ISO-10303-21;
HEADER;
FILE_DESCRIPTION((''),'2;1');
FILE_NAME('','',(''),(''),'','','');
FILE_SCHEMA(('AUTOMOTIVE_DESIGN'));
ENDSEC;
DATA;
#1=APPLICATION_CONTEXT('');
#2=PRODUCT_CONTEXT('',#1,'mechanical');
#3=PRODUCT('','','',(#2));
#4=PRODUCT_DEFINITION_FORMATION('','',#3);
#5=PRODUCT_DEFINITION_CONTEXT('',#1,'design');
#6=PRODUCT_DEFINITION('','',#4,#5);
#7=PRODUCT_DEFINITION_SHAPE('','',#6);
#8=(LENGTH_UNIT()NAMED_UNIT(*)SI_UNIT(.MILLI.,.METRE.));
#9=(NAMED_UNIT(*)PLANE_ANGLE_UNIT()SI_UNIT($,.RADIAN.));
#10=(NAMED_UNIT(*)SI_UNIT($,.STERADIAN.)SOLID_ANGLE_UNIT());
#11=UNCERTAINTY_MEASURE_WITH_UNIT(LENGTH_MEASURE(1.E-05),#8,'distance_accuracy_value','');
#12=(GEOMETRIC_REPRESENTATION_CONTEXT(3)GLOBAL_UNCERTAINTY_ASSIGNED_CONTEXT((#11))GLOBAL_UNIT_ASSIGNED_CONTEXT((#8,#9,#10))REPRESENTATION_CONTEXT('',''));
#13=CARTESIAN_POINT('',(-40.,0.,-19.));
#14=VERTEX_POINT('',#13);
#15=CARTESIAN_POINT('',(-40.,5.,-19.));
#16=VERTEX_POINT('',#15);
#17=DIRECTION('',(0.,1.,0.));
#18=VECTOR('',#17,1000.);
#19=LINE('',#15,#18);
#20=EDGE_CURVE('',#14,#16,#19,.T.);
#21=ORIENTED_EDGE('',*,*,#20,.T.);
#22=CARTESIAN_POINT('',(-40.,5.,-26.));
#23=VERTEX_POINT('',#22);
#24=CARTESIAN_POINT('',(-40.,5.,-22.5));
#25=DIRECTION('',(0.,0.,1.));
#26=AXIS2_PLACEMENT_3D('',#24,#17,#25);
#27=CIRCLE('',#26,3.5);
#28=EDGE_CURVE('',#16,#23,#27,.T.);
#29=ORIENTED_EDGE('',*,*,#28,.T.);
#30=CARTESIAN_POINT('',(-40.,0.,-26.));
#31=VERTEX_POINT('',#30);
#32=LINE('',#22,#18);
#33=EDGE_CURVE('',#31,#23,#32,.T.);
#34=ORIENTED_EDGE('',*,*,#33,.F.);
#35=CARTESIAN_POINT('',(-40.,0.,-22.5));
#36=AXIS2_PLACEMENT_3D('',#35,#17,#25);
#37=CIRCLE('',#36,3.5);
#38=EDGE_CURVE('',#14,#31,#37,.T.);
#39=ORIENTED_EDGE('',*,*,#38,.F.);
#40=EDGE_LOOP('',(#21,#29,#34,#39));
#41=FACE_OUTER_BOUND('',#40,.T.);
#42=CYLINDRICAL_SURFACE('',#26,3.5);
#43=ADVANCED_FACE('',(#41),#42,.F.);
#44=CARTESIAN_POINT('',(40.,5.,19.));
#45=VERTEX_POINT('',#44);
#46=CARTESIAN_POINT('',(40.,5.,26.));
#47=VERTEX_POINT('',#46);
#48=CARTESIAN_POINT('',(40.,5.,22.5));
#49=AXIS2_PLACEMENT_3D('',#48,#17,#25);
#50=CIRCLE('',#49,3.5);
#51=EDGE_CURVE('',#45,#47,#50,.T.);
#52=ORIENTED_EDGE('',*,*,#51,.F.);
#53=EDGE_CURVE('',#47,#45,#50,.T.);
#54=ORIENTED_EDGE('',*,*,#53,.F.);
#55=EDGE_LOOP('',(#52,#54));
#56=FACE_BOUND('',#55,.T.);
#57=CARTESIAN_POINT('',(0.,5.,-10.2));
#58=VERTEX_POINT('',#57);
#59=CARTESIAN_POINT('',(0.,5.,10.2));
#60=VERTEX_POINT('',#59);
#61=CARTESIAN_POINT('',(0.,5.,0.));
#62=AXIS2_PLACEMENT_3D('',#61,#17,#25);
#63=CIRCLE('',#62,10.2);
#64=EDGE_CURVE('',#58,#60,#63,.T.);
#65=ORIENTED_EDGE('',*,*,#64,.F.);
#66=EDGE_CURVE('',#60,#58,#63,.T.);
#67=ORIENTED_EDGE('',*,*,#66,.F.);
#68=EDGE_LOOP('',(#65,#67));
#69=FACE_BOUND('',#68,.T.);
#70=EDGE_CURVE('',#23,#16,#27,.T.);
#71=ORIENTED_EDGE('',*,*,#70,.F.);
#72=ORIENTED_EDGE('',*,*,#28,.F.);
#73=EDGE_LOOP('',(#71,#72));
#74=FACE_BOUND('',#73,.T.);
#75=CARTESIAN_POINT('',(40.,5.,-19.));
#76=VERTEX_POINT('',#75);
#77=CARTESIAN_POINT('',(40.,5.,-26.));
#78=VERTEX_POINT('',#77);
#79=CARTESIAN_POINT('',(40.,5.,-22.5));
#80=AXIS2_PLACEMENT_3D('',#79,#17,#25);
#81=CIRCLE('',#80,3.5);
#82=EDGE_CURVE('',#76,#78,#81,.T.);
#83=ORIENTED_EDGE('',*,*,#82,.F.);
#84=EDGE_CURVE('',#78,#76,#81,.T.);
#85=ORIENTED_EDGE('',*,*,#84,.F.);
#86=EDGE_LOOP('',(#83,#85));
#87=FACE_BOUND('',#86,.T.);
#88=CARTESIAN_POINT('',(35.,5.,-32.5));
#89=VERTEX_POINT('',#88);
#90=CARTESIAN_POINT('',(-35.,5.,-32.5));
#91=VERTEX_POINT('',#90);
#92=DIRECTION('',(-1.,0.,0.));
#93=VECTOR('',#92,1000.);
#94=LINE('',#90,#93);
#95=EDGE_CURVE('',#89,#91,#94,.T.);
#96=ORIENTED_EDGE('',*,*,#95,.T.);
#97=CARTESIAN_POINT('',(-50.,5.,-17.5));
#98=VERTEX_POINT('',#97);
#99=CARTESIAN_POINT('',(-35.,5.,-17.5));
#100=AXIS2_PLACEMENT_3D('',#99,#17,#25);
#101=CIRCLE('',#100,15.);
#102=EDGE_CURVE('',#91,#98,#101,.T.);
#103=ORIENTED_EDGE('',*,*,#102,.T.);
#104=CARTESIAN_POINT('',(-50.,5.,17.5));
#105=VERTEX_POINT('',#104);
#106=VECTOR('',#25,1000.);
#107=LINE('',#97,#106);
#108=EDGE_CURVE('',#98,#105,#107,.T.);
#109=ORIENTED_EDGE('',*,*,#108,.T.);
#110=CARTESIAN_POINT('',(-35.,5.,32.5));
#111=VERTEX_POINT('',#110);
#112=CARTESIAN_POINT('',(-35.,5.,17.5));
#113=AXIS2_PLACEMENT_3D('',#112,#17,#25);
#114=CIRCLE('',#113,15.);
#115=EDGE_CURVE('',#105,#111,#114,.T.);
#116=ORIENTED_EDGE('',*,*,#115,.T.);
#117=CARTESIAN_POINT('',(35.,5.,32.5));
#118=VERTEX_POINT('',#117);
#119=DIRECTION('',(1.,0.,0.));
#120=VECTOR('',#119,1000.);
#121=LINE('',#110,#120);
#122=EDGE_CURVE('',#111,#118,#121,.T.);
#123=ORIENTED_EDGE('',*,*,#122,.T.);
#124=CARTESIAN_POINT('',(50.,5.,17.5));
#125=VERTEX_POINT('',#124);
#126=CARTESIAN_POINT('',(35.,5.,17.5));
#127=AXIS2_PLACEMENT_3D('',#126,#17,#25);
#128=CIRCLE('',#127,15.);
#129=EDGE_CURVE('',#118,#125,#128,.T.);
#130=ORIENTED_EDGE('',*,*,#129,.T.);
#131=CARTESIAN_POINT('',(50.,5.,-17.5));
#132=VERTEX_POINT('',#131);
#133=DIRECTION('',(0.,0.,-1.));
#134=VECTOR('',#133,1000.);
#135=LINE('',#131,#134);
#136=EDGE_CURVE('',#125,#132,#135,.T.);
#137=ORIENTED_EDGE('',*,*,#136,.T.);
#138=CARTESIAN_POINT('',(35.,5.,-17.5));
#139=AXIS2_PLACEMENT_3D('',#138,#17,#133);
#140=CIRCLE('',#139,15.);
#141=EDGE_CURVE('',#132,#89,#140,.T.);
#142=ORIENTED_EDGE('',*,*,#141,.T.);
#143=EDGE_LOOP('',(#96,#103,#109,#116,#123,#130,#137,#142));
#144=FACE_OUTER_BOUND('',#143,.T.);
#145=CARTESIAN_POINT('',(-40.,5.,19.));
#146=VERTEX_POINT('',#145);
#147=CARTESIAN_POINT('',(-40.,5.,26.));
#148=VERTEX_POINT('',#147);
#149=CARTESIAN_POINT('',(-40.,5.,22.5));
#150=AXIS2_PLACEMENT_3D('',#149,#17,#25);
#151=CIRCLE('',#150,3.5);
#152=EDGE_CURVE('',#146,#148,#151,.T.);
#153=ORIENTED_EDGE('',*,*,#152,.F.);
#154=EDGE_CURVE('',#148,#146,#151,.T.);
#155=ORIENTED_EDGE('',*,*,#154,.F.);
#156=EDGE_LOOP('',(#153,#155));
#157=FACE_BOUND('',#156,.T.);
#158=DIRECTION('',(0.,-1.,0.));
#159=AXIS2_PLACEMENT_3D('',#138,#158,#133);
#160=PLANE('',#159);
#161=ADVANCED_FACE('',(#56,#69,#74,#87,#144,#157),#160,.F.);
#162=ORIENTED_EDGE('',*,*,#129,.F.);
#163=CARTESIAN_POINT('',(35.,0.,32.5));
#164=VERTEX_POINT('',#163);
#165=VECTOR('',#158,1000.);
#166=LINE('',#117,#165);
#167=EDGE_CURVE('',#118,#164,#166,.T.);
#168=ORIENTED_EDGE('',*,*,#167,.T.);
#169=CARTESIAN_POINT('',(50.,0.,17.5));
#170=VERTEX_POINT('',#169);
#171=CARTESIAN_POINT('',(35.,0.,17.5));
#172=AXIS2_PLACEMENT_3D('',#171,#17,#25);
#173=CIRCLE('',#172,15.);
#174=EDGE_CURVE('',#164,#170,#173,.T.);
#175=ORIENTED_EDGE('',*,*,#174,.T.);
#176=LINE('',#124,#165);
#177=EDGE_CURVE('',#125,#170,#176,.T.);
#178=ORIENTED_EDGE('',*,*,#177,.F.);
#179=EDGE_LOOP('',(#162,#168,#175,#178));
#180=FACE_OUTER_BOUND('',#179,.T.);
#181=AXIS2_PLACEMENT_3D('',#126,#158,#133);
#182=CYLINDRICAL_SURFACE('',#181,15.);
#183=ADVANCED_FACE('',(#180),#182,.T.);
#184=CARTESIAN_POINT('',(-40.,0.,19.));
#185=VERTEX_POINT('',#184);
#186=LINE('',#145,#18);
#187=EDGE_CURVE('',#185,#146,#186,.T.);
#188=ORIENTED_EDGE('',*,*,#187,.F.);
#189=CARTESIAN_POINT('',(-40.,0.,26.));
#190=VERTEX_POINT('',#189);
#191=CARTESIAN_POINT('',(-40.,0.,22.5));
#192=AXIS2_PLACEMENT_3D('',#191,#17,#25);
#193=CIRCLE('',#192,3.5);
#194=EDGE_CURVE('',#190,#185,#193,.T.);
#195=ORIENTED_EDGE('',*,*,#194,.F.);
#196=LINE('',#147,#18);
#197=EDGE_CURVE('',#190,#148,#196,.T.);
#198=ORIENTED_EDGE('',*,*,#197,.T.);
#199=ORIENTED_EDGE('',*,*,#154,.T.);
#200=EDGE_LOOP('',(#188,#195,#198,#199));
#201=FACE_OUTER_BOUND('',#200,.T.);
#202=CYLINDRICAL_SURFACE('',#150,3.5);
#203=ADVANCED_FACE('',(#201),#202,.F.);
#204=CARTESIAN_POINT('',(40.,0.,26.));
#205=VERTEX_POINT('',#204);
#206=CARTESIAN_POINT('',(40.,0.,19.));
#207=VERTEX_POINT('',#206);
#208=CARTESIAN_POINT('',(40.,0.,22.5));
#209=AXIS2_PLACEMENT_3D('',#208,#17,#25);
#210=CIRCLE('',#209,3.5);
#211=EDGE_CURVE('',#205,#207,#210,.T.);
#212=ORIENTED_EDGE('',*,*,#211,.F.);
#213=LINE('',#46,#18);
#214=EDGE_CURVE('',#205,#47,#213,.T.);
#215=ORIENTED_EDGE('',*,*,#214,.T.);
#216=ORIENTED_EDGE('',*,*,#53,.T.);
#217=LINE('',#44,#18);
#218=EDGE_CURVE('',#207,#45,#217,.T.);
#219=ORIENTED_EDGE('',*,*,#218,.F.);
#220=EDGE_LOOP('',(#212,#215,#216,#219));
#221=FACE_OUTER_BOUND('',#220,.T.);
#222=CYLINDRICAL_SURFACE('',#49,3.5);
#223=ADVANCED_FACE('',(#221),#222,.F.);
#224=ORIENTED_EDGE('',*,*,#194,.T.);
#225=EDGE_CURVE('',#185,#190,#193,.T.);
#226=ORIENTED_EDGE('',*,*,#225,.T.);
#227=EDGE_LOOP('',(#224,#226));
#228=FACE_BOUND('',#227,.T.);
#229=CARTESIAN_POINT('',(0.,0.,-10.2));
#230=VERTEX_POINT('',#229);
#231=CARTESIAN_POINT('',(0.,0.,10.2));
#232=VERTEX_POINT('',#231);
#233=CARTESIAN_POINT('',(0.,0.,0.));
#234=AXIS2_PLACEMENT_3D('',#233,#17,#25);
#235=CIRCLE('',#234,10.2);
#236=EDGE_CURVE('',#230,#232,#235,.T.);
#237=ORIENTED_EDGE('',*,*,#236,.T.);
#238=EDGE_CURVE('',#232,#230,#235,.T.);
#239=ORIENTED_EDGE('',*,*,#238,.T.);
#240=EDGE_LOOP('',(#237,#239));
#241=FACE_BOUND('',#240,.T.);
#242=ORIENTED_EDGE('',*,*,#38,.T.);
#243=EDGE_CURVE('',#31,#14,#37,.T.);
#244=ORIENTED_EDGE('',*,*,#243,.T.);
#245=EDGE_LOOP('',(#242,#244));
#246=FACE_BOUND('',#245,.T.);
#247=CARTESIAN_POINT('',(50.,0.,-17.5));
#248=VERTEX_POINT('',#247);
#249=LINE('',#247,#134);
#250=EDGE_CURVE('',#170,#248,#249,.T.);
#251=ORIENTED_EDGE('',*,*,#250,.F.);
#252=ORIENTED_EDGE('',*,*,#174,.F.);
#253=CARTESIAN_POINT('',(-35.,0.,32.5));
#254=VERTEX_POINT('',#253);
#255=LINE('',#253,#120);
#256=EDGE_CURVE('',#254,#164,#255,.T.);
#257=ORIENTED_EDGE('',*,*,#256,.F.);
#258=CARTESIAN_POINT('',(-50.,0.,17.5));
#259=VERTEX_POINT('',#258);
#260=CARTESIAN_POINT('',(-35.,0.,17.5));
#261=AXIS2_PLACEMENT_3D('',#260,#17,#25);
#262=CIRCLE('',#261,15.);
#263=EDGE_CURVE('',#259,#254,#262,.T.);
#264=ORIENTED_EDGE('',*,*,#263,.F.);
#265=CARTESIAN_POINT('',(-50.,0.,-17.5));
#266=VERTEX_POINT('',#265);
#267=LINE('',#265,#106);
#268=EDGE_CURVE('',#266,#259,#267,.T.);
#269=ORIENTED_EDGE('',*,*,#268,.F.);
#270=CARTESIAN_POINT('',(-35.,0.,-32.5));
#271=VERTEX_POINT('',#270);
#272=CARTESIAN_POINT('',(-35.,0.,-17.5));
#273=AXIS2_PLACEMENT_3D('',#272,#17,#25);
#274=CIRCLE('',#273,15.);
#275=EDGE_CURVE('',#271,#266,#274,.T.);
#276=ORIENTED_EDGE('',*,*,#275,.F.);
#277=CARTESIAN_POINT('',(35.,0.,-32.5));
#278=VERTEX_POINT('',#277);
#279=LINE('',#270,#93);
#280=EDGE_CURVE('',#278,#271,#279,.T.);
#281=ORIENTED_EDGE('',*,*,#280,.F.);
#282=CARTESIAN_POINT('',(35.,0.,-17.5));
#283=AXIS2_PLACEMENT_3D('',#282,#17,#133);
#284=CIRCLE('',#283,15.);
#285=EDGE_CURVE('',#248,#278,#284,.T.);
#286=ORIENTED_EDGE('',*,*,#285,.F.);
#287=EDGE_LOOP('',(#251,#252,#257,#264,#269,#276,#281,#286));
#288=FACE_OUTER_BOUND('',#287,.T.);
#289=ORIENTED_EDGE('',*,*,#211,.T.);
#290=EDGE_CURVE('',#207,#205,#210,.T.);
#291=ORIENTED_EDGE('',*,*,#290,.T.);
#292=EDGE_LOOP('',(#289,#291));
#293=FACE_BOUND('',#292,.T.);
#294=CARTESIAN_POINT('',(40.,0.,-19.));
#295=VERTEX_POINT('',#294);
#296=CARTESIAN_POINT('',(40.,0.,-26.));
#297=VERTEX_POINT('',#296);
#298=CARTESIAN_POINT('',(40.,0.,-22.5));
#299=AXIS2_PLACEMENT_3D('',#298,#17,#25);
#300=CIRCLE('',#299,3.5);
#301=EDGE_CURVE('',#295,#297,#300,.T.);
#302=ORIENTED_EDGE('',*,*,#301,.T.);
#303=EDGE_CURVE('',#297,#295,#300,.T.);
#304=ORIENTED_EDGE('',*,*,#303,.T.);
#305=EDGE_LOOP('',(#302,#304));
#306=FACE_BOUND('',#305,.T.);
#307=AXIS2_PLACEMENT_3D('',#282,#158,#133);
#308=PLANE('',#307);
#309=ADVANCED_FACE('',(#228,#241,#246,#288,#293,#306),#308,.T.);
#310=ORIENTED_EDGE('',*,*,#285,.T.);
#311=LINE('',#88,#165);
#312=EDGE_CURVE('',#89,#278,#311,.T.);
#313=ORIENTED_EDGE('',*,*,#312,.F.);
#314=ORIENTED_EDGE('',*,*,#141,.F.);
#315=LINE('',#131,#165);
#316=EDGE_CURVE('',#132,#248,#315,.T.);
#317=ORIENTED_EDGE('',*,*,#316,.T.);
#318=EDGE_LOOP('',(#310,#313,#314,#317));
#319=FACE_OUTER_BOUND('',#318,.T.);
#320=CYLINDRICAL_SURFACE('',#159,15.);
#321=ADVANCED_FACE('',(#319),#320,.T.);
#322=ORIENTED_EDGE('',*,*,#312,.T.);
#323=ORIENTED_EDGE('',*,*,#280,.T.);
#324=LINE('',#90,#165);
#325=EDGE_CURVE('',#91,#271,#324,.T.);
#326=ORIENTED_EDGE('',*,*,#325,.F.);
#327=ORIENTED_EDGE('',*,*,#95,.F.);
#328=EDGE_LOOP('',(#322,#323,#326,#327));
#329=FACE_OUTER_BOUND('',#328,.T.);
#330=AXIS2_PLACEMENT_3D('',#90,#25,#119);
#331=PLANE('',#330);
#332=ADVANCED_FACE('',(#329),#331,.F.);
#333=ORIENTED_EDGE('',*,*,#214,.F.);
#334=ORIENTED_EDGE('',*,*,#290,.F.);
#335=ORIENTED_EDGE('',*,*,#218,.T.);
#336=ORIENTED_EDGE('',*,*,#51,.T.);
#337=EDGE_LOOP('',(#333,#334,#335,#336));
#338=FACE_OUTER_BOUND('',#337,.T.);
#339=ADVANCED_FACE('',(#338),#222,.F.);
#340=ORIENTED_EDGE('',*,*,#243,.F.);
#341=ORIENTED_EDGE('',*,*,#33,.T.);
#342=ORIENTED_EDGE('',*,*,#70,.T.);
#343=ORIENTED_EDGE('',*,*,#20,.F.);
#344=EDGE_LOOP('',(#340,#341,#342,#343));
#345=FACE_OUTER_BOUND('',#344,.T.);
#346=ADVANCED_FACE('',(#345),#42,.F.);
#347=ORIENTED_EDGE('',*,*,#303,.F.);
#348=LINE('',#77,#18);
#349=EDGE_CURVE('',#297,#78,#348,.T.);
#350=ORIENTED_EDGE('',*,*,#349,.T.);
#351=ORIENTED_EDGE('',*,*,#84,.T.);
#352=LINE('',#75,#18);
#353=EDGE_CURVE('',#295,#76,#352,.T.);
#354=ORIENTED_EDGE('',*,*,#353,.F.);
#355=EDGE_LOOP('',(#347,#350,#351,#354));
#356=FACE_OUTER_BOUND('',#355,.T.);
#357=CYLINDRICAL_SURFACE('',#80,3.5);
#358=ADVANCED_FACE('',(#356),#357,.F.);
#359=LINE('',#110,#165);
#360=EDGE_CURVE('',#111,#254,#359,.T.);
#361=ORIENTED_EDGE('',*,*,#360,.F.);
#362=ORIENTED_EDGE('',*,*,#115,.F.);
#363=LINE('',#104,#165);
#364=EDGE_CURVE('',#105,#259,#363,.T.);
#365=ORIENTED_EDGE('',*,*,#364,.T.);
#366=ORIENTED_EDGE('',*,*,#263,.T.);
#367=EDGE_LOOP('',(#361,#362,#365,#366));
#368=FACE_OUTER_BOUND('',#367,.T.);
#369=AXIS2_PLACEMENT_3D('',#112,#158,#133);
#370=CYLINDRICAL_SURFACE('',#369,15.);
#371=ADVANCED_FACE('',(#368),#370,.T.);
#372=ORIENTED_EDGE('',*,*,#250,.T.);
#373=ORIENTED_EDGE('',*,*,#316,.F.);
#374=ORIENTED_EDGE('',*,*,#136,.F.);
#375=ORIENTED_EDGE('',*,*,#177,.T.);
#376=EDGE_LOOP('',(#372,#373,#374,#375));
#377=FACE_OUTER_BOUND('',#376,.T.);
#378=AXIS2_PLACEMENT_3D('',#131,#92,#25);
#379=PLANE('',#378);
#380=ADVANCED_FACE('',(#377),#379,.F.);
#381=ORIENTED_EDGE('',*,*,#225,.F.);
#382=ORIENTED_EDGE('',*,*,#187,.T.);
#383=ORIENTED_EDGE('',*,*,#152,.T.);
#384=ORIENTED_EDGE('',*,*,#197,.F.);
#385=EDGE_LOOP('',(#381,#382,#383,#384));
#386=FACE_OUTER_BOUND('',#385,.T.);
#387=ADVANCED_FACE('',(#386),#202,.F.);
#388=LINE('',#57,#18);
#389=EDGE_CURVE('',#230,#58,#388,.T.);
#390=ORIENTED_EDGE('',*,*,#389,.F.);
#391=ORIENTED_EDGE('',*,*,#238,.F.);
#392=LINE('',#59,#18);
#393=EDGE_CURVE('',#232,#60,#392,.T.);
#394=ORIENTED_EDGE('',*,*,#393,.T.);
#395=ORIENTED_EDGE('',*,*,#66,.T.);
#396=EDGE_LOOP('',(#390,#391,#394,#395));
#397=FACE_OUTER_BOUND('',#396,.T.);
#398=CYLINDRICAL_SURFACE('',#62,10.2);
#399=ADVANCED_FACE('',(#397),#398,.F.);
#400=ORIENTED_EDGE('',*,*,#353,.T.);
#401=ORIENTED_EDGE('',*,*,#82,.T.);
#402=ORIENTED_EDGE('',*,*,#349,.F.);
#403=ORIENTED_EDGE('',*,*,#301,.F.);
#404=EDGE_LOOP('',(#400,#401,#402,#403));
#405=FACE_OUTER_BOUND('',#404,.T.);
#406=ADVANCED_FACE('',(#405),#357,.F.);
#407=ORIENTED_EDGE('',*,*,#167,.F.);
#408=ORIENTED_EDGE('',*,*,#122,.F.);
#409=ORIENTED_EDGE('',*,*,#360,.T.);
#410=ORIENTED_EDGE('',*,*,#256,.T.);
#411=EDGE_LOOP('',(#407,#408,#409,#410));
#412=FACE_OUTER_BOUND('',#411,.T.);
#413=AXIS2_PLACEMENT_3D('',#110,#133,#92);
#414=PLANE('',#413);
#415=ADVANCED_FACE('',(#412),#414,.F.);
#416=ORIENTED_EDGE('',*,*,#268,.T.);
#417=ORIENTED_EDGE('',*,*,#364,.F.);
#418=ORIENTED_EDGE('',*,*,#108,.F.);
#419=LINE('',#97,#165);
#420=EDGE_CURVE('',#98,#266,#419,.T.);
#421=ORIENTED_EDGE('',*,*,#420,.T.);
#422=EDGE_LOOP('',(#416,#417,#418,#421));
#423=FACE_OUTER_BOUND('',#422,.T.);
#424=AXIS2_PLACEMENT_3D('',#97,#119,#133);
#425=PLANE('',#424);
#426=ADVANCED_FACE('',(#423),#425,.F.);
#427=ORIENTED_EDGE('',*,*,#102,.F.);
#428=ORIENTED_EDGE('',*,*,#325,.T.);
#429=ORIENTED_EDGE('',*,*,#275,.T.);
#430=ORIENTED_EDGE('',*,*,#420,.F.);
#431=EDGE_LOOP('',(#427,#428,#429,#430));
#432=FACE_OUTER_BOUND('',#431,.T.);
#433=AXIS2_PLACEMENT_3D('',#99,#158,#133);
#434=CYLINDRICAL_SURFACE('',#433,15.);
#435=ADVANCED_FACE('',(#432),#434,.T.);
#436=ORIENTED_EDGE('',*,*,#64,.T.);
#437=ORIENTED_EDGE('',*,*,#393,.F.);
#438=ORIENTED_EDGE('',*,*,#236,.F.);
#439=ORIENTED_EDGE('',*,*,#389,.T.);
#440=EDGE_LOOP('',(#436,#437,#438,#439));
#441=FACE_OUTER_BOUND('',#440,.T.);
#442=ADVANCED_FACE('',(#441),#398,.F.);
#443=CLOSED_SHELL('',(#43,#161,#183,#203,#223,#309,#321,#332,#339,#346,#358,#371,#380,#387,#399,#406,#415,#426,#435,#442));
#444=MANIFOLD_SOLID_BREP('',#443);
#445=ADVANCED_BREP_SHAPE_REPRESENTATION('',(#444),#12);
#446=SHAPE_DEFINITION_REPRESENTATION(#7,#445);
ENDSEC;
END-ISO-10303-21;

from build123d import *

# Parameters (mm, degrees)
BOSS_EXTRUDE1_DEPTH          = 5
M24_TAPPED_HOLE2_D           = 20.4
M24_TAPPED_HOLE2_ON_FACE_2_D = 20.4
HOLE1_D                      = 7
LPATTERN1_COUNT              = 2
LPATTERN1_PITCH              = 80
LPATTERN1_COUNT_DIR2         = 2
LPATTERN1_PITCH_DIR2         = 45


with BuildPart() as part:
    # Sketch1 → Boss-Extrude1 (new body)
    with BuildSketch(Plane(origin=(0, 0, 0), x_dir=(1, 0, 0), z_dir=(0, 1, 0))):
        with BuildLine():
            Line((-35, 32.5), (35, 32.5))
            ThreePointArc((35, 32.5), (45.606601718, 28.106601718), (50, 17.5))
            Line((50, 17.5), (50, -17.5))
            ThreePointArc((50, -17.5), (45.606601718, -28.106601718), (35, -32.5))
            Line((35, -32.5), (-35, -32.5))
            ThreePointArc((-35, -32.5), (-45.606601718, -28.106601718), (-50, -17.5))
            Line((-50, -17.5), (-50, 17.5))
            ThreePointArc((-50, 17.5), (-45.606601718, 28.106601718), (-35, 32.5))
        make_face()
    extrude(amount=BOSS_EXTRUDE1_DEPTH)

    # M24 Tapped Hole2 (through all)
    with Locations(Plane(origin=(0, 0, 0), x_dir=(0, 0, -1), z_dir=(0, -1, 0))):
        with Locations((0, 0)):
            Hole(M24_TAPPED_HOLE2_D / 2)

    # M24 Tapped Hole2 on face 2 (through all)
    with Locations(Plane.ZX.offset(5)):
        with Locations((0, 0)):
            Hole(M24_TAPPED_HOLE2_ON_FACE_2_D / 2)

    # Hole1 (through all)
    with Locations(Plane(origin=(-40, 5, -22.5), x_dir=(0, 0, 1), z_dir=(0, 1, 0))):
        with Locations((0, 0)):
            hole1 = Hole(HOLE1_D / 2)

    # LPattern1: Hole1 2 × 2
    with Locations(*[(i * LPATTERN1_PITCH, 0, j * LPATTERN1_PITCH_DIR2) for i in range(LPATTERN1_COUNT) for j in range(LPATTERN1_COUNT_DIR2) if (i, j) != (0, 0)]):
        add(hole1, mode=Mode.SUBTRACT)


solid = part.part
